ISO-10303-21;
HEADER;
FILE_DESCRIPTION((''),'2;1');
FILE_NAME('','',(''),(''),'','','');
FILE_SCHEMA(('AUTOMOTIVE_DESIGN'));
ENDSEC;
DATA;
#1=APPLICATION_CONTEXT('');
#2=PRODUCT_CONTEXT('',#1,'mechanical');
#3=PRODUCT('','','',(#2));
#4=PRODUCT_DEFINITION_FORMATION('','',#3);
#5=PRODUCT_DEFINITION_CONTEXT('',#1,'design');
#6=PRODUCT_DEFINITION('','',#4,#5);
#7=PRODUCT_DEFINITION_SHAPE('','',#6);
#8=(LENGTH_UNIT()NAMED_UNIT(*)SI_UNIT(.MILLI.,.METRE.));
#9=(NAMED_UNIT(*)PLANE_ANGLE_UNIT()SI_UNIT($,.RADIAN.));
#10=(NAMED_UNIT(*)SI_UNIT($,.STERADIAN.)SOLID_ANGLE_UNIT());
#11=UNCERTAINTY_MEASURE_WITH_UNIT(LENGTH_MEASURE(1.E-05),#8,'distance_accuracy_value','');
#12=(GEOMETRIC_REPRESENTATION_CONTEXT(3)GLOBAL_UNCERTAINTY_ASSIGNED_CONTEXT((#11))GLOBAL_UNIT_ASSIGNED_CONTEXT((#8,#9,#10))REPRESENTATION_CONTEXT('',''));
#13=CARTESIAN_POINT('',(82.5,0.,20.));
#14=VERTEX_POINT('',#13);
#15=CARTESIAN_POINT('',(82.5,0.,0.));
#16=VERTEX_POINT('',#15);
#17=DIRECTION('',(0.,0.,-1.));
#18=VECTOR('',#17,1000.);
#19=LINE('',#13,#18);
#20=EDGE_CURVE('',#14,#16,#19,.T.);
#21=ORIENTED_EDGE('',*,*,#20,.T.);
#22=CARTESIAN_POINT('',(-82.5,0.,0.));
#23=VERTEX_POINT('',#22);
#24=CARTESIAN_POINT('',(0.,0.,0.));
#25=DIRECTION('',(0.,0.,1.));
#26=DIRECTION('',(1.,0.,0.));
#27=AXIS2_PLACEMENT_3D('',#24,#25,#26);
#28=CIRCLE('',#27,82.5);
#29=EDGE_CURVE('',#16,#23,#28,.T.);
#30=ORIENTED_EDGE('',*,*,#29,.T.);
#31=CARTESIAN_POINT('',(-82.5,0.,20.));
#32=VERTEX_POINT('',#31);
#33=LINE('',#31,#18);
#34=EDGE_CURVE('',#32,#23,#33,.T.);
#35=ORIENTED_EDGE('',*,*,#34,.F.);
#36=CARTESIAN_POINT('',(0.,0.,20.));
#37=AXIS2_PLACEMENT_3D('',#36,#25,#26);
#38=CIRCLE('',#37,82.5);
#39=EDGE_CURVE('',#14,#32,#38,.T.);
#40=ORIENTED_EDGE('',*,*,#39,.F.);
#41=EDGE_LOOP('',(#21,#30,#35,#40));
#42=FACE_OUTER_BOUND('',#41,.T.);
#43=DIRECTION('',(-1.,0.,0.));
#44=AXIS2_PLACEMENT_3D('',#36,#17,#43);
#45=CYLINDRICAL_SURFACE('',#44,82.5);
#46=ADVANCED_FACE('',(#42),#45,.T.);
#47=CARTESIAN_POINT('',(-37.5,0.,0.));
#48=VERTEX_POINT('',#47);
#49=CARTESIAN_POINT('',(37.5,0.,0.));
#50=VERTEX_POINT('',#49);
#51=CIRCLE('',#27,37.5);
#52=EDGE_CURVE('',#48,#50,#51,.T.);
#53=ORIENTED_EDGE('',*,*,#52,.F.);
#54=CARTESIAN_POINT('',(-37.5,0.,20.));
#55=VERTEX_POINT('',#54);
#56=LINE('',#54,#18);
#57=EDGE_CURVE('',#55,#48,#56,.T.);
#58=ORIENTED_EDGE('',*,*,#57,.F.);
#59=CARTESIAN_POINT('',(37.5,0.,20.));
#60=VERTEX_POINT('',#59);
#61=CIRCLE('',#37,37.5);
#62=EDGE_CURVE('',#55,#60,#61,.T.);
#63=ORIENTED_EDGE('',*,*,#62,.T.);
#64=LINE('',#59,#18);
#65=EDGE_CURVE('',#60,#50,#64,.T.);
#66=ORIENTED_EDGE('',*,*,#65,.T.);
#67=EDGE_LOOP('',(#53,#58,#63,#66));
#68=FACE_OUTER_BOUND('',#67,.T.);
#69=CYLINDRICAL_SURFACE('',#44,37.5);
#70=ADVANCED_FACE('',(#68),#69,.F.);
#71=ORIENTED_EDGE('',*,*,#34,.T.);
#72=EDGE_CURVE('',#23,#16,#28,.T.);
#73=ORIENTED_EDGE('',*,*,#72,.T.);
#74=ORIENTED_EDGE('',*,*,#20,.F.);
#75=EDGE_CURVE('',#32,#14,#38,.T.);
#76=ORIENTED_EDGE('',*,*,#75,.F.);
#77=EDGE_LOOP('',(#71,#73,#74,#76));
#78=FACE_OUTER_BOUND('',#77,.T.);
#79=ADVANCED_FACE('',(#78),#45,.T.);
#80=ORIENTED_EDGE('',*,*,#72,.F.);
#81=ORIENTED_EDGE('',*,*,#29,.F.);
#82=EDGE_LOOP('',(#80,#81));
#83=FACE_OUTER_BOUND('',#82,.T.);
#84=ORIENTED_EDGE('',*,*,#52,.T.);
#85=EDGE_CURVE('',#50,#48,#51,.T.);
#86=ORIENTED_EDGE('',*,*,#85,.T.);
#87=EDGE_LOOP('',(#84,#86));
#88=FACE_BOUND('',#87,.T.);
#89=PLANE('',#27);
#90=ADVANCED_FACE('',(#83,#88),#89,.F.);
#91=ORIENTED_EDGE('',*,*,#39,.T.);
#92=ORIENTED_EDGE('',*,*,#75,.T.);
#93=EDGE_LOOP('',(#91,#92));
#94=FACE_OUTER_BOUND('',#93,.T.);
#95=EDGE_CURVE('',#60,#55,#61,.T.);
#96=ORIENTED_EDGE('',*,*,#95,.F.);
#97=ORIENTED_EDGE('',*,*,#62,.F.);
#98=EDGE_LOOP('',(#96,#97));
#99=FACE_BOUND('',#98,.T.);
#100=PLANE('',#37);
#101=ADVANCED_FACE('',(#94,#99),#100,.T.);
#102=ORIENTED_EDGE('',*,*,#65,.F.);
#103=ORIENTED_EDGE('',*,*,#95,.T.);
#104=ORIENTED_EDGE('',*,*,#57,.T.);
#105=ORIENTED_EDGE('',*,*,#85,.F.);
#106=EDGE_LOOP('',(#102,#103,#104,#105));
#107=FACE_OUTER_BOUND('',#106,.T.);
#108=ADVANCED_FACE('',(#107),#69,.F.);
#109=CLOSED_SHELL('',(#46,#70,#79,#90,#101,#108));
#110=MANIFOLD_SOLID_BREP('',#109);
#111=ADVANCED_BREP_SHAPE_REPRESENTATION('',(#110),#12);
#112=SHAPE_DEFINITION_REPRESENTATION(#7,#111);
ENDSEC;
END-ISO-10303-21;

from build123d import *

# Parameters (mm, degrees)
SKETCH1_R           = 82.5
SKETCH1_R_2         = 37.5
BOSS_EXTRUDE1_DEPTH = 20


with BuildPart() as part:
    # Sketch1 → Boss-Extrude1 (new body)
    with BuildSketch(Plane.XY):
        Circle(SKETCH1_R)
        Circle(SKETCH1_R_2, mode=Mode.SUBTRACT)
    extrude(amount=BOSS_EXTRUDE1_DEPTH)


solid = part.part
